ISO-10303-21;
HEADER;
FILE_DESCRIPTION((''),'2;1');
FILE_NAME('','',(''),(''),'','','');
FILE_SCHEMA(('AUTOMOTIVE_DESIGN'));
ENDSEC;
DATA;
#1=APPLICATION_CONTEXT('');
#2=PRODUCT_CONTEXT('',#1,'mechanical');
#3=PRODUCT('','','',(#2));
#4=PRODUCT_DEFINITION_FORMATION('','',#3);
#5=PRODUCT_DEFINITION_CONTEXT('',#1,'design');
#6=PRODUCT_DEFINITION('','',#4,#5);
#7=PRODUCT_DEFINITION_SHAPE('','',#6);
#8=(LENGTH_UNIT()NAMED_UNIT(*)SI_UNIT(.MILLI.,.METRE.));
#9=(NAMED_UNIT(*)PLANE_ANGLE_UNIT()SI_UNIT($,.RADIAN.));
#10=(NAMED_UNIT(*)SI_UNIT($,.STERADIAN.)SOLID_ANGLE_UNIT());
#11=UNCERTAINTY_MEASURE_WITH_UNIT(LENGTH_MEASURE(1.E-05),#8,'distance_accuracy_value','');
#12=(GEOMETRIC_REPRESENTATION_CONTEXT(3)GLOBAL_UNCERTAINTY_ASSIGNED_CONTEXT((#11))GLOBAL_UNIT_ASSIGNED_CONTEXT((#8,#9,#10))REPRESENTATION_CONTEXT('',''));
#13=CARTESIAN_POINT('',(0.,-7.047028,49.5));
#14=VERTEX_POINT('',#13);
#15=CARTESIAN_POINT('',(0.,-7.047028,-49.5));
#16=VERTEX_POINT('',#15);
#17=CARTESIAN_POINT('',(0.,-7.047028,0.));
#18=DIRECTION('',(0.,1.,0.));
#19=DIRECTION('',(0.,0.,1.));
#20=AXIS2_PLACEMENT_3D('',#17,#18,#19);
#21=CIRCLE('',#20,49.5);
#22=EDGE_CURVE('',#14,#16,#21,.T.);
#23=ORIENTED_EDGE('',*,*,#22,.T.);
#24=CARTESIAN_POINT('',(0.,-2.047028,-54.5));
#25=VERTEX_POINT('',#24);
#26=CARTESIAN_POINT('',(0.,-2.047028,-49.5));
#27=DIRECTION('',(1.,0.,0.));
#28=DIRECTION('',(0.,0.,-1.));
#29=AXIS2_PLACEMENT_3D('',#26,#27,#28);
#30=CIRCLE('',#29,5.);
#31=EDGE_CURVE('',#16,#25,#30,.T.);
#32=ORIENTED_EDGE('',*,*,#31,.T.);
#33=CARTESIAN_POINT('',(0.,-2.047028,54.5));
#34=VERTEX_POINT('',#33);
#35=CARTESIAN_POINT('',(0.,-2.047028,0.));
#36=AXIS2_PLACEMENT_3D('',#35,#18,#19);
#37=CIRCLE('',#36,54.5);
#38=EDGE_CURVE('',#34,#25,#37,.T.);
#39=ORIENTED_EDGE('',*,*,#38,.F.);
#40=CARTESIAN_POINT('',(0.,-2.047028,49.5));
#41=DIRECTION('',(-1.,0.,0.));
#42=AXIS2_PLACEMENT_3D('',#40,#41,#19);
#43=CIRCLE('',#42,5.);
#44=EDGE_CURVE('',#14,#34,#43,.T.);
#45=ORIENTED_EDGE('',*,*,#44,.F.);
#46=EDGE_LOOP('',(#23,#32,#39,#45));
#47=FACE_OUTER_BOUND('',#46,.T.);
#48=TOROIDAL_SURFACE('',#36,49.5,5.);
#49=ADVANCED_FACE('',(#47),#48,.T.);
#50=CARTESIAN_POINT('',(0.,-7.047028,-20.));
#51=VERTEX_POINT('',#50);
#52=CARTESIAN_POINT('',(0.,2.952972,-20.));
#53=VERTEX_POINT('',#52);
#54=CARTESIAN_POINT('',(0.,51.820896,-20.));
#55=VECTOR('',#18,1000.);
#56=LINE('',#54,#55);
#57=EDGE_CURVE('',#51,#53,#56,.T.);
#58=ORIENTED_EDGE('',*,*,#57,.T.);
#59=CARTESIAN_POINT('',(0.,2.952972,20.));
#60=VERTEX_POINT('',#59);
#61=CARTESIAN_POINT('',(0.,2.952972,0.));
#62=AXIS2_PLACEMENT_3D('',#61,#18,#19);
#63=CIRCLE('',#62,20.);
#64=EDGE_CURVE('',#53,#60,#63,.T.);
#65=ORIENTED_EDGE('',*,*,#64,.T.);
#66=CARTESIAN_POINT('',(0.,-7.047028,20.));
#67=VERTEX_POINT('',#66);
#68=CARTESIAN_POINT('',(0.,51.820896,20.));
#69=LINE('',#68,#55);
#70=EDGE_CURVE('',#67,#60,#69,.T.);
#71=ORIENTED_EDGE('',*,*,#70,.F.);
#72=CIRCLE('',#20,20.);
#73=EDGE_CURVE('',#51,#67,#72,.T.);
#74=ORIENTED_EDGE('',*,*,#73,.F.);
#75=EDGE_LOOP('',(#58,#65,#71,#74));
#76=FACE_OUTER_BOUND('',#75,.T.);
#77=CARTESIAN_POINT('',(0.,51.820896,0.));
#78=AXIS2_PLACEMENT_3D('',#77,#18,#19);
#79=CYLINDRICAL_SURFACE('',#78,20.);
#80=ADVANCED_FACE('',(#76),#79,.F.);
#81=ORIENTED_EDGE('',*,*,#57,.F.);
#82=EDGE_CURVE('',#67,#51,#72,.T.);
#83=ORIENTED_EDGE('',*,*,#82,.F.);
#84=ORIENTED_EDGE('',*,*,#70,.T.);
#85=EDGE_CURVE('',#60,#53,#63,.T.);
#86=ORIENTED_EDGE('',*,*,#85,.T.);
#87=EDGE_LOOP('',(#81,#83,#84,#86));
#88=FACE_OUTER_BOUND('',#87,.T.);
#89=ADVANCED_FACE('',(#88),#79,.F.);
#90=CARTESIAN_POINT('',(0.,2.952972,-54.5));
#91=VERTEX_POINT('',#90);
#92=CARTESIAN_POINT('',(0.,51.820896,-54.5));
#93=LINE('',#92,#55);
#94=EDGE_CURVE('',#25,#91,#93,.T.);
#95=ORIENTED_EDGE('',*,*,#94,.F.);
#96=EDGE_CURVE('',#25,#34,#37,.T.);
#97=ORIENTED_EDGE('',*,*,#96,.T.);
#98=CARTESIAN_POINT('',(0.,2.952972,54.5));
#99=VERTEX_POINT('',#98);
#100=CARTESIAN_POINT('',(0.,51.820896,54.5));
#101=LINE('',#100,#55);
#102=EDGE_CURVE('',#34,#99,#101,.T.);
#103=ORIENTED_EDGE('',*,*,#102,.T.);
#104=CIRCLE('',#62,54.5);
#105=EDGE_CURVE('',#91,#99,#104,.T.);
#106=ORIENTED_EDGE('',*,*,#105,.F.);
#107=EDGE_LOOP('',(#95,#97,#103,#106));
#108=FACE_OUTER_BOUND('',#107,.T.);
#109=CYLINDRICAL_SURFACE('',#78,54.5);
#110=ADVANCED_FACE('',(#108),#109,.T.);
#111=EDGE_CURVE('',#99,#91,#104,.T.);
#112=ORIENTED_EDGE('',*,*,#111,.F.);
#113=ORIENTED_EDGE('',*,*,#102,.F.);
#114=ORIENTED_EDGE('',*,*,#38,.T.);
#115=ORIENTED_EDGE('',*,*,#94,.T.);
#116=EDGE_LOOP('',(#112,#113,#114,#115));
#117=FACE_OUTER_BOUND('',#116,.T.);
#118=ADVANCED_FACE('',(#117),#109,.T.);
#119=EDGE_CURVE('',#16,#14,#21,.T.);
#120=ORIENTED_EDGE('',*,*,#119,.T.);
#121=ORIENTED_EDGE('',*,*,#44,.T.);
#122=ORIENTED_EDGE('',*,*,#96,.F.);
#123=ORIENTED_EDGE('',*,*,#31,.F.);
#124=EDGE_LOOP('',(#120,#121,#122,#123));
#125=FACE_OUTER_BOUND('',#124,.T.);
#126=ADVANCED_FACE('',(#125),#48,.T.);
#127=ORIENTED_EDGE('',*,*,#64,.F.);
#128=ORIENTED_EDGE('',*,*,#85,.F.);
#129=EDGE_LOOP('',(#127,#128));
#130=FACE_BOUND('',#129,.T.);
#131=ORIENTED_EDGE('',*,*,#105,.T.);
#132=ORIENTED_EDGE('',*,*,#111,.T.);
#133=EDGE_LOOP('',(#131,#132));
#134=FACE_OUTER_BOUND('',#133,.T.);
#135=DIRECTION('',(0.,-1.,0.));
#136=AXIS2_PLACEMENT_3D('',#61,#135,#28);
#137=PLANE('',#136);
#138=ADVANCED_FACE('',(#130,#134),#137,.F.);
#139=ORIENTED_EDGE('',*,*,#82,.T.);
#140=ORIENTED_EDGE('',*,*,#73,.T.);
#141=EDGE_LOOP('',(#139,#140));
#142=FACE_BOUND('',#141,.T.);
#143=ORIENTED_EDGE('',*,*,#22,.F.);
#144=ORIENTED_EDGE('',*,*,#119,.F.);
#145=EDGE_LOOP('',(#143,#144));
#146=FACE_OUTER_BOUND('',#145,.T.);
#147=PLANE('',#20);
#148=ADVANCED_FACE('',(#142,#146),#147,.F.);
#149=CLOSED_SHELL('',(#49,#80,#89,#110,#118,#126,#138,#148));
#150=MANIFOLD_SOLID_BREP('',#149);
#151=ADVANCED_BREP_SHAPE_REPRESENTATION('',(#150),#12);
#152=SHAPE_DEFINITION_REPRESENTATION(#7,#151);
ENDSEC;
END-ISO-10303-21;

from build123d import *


with BuildPart() as part:
    # 草图1 → 旋转1 (revolve)
    with BuildSketch(Plane.XY, mode=Mode.PRIVATE) as revolve_1_sk:
        with BuildLine():
            Line((20, -7.047028188), (49.5, -7.047028188))
            ThreePointArc((49.5, -7.047028188), (53.035533906, -5.582562094), (54.5, -2.047028188))
            Line((54.5, -2.047028188), (54.5, 2.952971812))
            Line((54.5, 2.952971812), (20, 2.952971812))
            Line((20, 2.952971812), (20, -7.047028188))
        make_face()
    revolve(revolve_1_sk.sketch.rotate(Axis((0, 51.82089634, 0), (0, -1, 0)), 90), axis=Axis((0, 51.82089634, 0), (0, -1, 0)))


solid = part.part
